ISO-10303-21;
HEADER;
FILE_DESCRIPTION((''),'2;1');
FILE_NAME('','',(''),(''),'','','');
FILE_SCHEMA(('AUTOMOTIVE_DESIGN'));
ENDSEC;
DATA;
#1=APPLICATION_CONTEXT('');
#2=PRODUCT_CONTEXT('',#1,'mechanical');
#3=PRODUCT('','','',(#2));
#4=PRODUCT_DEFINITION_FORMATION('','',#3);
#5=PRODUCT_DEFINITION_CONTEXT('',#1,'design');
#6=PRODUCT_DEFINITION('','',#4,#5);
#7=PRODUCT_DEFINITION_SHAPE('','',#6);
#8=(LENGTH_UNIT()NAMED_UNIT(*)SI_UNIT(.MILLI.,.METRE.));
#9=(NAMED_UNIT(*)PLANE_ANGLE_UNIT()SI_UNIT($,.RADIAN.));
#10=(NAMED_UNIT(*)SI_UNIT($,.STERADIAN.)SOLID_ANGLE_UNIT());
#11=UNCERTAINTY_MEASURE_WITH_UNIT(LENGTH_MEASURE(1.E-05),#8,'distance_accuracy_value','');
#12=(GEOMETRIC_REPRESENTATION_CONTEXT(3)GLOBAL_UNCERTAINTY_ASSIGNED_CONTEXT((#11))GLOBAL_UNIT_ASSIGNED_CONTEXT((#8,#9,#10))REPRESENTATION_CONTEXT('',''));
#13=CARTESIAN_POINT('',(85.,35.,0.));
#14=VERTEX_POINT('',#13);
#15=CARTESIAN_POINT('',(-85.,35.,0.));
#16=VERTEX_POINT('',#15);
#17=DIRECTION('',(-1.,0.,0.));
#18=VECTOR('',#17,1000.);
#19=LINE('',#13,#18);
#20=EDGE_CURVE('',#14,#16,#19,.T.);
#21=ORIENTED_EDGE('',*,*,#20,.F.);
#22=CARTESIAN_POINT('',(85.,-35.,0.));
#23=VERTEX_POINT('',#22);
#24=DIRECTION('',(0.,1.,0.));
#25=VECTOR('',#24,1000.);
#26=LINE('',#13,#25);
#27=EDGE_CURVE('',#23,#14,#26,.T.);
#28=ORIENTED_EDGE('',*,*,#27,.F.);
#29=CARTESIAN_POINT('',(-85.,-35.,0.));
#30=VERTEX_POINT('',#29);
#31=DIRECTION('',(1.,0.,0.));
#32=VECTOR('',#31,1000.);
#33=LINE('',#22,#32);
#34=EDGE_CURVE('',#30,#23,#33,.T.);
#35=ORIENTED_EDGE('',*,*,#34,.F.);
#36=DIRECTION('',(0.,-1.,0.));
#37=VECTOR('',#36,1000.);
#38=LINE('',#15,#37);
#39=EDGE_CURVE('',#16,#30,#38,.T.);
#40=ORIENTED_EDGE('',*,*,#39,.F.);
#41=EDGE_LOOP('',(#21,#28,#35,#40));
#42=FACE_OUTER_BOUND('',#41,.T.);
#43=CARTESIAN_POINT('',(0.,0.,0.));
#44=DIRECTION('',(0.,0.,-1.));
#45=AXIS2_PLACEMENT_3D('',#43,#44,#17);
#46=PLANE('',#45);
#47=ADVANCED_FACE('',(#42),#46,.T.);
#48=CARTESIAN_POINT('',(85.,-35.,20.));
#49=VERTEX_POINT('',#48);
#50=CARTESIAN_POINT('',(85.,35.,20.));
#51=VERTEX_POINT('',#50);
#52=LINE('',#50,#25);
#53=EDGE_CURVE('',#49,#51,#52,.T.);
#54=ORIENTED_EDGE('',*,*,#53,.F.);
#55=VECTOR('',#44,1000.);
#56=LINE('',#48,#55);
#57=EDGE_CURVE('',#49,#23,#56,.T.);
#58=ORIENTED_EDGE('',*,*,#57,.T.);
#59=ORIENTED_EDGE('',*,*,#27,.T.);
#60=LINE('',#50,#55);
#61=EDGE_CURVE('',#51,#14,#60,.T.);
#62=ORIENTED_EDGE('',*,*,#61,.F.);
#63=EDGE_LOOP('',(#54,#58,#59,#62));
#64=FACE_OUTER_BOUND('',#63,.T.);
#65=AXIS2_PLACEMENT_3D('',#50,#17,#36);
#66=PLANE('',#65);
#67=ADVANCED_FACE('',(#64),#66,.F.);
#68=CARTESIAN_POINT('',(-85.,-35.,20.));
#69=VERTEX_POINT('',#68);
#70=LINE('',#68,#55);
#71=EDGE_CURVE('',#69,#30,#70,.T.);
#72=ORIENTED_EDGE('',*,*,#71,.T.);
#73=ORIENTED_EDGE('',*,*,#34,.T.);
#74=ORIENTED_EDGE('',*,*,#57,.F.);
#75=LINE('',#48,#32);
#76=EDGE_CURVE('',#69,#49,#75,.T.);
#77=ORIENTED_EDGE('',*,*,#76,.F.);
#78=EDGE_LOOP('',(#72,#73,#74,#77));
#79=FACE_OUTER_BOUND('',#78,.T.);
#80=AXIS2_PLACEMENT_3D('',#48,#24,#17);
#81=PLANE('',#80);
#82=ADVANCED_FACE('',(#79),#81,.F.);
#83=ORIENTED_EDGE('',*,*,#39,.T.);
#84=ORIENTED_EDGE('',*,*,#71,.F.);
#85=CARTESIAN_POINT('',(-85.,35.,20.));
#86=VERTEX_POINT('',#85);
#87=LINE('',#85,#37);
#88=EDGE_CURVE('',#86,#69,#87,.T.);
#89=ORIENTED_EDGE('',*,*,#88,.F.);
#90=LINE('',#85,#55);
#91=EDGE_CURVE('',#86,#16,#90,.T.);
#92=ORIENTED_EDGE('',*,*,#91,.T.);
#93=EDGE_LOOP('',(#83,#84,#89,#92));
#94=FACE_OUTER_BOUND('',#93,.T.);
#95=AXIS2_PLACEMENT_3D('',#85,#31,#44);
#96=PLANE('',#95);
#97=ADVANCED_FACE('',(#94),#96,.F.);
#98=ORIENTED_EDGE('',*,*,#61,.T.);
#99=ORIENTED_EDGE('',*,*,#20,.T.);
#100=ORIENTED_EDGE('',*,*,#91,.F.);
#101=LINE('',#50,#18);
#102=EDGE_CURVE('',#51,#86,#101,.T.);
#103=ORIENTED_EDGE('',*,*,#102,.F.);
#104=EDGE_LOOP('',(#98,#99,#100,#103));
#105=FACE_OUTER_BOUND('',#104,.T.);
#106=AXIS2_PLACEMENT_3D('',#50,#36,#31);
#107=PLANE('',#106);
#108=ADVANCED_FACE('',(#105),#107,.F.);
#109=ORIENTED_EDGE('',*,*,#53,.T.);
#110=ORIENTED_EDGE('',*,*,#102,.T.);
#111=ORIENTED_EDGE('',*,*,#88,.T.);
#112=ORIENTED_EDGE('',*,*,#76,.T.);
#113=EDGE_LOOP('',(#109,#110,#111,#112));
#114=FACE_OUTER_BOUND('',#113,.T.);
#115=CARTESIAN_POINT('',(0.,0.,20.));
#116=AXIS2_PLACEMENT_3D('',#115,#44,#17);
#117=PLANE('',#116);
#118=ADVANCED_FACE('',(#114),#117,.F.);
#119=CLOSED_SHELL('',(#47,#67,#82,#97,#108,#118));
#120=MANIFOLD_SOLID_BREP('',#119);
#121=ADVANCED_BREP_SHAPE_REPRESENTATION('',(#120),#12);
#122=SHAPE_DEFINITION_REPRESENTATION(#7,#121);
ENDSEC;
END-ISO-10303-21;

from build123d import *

# Parameters (mm, degrees)
SKETCH_1_W      = 170
SKETCH_1_H      = 70
EXTRUDE_1_DEPTH = 20


with BuildPart() as part:
    # 草图1 → 凸台-拉伸1 (new body)
    with BuildSketch(Plane.XY):
        Rectangle(SKETCH_1_W, SKETCH_1_H)
    extrude(amount=EXTRUDE_1_DEPTH)


solid = part.part
